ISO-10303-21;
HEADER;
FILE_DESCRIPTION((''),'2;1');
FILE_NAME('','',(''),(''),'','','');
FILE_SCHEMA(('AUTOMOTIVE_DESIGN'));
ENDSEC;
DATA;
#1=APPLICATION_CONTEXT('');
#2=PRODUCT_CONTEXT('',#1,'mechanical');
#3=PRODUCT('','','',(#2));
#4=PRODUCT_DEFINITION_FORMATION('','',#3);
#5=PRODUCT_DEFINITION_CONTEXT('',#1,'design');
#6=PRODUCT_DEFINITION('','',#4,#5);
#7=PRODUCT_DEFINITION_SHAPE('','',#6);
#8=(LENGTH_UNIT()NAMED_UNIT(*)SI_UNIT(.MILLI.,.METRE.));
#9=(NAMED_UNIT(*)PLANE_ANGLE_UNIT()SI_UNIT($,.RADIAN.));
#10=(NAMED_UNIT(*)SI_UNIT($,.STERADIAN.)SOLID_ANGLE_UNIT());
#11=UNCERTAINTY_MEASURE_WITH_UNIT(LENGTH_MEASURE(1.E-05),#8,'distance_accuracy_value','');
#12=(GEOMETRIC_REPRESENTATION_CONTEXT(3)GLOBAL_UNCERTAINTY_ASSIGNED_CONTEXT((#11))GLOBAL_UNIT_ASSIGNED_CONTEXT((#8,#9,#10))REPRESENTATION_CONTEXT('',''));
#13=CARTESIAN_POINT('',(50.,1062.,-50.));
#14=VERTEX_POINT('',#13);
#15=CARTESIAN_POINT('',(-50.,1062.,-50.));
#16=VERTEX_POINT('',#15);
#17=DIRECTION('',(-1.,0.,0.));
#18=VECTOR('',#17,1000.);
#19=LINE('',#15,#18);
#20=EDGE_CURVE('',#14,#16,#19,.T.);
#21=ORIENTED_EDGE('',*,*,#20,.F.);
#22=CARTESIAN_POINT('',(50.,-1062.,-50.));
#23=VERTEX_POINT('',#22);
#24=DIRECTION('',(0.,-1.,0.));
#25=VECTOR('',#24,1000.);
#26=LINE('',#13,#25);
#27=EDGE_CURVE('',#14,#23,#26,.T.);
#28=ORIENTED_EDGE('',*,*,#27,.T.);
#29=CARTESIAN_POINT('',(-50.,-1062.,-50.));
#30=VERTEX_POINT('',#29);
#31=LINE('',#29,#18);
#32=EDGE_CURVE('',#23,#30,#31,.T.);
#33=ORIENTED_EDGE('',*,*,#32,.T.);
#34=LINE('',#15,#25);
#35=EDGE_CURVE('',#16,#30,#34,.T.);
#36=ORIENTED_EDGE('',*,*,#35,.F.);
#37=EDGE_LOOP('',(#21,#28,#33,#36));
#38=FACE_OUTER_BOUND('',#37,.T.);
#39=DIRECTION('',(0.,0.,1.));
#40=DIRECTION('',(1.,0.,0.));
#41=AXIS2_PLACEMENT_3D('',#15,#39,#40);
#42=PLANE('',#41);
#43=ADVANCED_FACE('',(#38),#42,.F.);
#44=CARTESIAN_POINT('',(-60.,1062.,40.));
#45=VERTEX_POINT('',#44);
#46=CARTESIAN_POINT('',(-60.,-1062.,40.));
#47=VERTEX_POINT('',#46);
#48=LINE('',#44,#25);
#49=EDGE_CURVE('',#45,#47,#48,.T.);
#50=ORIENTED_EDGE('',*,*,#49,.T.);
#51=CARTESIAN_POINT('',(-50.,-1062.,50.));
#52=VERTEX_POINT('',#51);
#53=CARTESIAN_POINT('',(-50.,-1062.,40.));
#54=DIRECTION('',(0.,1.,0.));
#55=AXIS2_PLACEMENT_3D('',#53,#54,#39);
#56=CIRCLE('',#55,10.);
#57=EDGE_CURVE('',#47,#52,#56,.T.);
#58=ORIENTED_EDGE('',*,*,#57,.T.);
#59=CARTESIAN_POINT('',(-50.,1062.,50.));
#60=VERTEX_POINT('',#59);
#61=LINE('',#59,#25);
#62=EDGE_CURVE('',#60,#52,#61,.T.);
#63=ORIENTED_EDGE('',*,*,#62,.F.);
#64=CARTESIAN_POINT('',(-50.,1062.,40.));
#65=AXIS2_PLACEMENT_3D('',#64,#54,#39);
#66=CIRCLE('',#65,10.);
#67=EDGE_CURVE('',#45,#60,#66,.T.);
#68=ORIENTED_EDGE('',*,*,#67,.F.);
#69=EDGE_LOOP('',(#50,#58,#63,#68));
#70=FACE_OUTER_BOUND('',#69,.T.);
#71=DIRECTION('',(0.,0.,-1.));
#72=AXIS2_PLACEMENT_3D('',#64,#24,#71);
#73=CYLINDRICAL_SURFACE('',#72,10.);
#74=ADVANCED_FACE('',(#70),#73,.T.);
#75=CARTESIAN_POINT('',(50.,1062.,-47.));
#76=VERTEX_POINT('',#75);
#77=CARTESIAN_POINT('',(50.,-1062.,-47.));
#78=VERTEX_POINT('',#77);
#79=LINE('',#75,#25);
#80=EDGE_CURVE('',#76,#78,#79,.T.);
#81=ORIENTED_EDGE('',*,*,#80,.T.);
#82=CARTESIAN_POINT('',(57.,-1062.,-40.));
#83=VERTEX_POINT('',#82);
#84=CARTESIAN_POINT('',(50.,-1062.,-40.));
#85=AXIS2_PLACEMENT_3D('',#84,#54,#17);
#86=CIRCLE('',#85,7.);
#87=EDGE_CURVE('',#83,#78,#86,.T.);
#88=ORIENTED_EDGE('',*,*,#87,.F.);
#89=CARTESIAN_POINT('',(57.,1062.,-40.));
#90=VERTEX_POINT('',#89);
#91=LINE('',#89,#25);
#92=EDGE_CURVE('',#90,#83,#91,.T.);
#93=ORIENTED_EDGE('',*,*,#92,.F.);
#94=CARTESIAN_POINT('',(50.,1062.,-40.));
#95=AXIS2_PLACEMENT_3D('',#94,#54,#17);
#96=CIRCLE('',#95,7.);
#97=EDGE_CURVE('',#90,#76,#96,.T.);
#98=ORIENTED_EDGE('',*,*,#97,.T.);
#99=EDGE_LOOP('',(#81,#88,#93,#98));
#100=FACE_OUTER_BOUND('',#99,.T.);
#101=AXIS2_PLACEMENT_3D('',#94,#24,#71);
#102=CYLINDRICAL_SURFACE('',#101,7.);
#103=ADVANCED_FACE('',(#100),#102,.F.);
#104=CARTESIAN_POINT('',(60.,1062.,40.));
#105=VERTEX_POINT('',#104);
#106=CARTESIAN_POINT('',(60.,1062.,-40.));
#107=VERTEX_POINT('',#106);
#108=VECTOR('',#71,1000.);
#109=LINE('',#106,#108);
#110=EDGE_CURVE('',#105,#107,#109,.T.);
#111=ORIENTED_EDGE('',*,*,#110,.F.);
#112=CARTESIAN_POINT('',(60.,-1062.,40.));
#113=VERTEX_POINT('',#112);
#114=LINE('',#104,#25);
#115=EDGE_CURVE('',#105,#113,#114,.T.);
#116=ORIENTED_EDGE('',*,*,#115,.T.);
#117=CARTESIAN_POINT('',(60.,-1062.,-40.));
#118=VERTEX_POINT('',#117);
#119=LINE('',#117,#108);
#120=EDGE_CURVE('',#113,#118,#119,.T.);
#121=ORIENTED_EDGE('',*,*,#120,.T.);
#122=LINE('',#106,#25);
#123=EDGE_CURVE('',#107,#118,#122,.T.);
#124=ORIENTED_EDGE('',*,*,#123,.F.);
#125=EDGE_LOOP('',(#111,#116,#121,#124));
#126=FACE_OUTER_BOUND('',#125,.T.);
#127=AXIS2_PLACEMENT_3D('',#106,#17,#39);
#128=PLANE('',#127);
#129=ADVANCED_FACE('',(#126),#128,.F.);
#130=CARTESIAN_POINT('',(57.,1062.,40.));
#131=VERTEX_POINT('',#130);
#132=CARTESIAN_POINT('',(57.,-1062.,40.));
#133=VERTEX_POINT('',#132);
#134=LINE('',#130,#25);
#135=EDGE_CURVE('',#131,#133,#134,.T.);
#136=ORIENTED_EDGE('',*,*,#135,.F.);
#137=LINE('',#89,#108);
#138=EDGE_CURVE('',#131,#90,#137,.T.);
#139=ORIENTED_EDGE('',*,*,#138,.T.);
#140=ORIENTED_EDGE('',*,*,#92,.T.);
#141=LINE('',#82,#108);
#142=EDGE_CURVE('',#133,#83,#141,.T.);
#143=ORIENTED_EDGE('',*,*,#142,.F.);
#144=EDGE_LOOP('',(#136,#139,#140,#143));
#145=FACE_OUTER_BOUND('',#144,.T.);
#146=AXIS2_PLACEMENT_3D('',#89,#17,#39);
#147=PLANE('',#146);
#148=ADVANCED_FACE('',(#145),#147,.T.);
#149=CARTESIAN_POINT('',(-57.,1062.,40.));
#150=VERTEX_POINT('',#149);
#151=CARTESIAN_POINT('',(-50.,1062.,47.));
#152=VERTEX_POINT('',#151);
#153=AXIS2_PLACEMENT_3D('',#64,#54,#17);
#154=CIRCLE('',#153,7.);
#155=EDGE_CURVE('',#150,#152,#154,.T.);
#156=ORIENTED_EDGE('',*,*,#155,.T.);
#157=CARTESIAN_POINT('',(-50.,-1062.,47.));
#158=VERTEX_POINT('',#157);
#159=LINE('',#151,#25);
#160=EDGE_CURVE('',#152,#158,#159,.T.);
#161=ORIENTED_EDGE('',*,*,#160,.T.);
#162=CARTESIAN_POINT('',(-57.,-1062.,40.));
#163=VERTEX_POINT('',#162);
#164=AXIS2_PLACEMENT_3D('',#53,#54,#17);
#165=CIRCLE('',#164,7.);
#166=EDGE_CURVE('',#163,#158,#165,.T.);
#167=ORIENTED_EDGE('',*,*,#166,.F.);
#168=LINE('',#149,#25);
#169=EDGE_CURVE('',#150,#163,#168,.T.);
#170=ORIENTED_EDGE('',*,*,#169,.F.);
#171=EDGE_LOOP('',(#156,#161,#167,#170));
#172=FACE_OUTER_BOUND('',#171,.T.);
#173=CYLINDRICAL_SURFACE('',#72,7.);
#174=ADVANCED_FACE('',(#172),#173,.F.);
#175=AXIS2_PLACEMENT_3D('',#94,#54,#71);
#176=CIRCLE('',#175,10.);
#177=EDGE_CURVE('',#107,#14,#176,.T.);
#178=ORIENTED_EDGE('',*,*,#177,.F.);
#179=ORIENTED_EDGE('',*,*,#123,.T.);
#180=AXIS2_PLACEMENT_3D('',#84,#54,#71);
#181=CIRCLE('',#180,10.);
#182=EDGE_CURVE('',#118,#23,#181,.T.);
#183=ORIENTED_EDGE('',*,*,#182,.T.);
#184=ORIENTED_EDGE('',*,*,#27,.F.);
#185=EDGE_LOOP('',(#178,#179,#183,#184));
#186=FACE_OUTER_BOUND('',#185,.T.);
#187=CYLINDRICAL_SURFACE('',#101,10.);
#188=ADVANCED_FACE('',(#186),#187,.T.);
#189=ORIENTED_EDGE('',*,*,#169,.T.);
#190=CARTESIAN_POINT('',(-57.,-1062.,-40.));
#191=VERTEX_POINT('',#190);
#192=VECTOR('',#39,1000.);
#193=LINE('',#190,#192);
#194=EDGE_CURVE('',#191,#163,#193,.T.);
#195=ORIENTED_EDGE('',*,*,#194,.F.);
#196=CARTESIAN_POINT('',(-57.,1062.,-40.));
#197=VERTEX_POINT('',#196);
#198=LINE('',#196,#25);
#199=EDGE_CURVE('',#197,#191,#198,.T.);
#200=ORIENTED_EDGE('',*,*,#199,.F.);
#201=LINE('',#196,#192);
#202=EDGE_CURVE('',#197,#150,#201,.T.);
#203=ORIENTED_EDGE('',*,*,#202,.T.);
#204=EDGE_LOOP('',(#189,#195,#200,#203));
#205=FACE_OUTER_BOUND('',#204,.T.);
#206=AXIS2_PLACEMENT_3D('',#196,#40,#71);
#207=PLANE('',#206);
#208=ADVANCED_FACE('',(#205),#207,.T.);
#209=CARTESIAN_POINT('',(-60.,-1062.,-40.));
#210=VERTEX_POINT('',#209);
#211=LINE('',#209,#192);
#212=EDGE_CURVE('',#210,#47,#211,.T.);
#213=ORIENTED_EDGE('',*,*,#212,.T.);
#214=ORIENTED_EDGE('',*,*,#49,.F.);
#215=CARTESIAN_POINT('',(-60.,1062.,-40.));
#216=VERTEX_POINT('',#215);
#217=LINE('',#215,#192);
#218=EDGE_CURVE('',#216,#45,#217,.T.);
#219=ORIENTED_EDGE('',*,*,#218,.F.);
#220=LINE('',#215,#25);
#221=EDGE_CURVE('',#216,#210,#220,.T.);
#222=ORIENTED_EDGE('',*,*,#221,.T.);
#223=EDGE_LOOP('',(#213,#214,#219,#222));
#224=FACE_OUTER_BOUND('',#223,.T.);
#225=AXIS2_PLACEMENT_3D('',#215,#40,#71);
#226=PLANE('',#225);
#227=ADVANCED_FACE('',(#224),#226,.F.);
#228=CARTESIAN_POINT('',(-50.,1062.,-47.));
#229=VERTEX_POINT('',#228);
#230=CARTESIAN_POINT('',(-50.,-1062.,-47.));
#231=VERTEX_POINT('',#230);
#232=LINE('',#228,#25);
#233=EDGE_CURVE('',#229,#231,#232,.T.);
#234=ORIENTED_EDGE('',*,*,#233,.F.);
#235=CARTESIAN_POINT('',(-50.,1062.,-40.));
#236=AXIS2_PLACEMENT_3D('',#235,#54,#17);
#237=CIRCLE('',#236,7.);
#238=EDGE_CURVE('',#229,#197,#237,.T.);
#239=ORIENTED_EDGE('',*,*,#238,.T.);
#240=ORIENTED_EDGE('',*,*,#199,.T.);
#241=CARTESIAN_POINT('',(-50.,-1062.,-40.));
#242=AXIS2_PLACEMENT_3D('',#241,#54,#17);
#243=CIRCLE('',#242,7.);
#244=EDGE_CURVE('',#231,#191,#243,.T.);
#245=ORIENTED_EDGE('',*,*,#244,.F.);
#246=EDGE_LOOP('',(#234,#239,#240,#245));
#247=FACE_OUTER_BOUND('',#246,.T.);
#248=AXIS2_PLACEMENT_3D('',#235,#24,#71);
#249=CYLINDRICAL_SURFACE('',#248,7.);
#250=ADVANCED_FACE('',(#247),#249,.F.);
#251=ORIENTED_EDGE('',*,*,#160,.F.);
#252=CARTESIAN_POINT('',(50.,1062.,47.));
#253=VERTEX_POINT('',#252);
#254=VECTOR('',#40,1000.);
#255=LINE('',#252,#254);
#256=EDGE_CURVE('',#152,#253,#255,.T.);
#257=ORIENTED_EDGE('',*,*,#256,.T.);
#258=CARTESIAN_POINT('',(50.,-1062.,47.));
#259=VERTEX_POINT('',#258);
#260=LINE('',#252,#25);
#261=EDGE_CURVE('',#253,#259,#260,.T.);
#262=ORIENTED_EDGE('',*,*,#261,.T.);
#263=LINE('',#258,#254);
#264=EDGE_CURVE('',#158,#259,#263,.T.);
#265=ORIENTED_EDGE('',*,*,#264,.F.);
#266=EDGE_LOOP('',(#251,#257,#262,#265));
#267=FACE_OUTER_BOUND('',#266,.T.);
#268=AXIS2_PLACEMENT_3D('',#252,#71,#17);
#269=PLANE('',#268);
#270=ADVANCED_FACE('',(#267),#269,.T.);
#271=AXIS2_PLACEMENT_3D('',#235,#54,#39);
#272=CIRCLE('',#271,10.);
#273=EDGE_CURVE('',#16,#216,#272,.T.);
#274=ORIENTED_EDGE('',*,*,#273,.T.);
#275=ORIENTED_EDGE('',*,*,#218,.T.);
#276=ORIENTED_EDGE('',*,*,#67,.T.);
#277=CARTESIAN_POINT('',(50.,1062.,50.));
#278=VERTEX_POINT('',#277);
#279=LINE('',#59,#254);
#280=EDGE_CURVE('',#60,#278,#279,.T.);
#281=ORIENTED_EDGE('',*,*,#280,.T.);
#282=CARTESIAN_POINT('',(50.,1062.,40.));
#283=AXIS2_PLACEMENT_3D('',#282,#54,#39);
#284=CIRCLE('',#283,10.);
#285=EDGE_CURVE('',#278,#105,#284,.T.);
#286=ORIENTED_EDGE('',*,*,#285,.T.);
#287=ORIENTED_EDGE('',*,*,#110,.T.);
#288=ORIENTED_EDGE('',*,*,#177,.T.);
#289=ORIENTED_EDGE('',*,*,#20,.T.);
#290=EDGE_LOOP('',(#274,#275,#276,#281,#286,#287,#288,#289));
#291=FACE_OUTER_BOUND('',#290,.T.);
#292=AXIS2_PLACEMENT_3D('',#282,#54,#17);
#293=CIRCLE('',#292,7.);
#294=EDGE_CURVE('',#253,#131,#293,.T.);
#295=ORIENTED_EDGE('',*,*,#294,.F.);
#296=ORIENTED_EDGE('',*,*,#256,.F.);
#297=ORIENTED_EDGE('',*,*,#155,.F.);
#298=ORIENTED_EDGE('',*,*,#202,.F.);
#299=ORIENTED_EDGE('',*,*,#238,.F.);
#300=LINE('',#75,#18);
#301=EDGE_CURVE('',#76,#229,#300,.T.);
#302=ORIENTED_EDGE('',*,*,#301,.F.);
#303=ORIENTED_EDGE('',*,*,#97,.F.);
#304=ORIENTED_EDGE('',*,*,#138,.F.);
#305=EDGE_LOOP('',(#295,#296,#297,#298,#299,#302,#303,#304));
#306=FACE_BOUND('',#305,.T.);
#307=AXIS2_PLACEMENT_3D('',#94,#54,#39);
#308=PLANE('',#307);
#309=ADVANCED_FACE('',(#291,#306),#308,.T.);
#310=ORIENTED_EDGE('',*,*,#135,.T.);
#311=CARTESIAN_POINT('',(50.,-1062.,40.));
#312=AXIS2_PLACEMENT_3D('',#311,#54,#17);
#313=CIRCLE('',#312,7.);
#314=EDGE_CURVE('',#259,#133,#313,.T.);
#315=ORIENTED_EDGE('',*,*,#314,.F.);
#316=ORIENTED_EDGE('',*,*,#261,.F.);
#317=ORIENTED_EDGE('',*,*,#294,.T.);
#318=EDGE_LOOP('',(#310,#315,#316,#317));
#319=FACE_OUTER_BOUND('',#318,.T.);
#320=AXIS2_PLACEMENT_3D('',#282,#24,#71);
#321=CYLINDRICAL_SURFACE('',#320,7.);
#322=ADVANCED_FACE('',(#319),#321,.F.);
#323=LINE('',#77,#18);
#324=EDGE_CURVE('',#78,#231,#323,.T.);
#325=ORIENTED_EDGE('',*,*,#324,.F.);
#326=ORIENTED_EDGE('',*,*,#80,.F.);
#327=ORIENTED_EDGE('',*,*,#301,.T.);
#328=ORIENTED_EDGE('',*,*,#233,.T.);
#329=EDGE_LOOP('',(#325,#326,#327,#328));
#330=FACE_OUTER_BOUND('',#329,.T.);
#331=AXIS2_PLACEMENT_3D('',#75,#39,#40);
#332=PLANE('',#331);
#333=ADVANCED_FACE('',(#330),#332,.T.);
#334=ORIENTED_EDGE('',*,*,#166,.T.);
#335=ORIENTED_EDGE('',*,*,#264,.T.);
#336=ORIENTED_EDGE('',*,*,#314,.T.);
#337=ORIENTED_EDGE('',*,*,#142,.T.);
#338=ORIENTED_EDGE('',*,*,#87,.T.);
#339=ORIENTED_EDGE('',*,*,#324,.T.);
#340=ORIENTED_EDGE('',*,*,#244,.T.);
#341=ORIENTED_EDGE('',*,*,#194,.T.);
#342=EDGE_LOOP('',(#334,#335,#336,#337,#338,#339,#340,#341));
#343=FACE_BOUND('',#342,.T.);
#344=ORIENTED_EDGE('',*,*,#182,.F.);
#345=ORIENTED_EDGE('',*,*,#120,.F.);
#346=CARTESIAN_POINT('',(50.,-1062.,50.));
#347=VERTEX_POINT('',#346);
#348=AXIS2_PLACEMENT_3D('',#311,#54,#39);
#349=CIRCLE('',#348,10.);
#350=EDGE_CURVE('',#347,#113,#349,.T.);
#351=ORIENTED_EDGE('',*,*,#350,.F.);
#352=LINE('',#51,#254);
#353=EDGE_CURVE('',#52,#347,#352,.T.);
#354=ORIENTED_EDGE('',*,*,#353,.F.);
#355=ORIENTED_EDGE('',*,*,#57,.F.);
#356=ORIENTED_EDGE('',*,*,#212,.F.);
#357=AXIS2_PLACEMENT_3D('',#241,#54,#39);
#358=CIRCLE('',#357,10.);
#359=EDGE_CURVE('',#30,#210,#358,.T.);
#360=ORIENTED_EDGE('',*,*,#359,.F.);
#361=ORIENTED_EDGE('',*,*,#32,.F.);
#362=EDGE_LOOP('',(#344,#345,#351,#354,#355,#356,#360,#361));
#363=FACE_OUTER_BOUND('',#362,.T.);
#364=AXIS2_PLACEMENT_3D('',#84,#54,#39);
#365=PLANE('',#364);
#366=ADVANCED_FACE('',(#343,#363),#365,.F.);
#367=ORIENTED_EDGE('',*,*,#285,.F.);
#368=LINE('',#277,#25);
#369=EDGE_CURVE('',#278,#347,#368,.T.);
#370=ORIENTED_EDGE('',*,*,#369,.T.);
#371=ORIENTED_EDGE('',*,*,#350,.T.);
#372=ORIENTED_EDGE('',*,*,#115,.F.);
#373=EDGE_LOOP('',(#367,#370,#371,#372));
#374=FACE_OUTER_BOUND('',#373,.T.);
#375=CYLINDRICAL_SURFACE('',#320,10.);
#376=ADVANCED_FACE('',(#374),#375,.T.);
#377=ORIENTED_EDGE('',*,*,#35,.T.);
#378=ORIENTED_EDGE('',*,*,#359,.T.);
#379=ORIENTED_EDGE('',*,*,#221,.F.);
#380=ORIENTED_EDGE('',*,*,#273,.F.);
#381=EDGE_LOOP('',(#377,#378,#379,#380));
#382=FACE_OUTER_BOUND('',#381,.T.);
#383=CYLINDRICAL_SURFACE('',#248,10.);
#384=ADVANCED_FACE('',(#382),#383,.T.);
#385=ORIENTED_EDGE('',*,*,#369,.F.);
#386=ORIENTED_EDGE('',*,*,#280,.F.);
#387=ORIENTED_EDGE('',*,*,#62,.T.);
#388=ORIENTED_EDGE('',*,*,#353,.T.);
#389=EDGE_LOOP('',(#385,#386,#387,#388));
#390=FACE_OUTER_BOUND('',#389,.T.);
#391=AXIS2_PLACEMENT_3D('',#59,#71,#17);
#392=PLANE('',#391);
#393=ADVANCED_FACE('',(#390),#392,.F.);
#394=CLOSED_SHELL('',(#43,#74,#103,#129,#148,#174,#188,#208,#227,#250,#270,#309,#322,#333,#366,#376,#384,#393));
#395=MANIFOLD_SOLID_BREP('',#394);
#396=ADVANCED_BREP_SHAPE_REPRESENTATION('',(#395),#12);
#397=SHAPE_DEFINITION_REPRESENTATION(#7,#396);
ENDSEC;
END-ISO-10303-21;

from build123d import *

# Parameters (mm, degrees)
EXTRUDE_THIN1_DEPTH = 1062


with BuildPart() as part:
    # Sketch1 → Extrude-Thin1 (new, symmetric)
    with BuildSketch(Plane(origin=(0, 0, 0), x_dir=(1, 0, 0), z_dir=(0, 1, 0))):
        with BuildLine():
            Line((-50, 50), (50, 50))
            ThreePointArc((50, 50), (57.071067812, 47.071067812), (60, 40))
            Line((60, 40), (60, -40))
            ThreePointArc((60, -40), (57.071067812, -47.071067812), (50, -50))
            Line((50, -50), (-50, -50))
            ThreePointArc((-50, -50), (-57.071067812, -47.071067812), (-60, -40))
            Line((-60, -40), (-60, 40))
            ThreePointArc((-60, 40), (-57.071067812, 47.071067812), (-50, 50))
        make_face()
        with BuildLine():
            Line((-50, 47), (50, 47))
            ThreePointArc((50, 47), (54.949747468, 44.949747468), (57, 40))
            Line((57, 40), (57, -40))
            ThreePointArc((57, -40), (54.949747468, -44.949747468), (50, -47))
            Line((50, -47), (-50, -47))
            ThreePointArc((-50, -47), (-54.949747468, -44.949747468), (-57, -40))
            Line((-57, -40), (-57, 40))
            ThreePointArc((-57, 40), (-54.949747468, 44.949747468), (-50, 47))
        make_face(mode=Mode.SUBTRACT)
    extrude(amount=EXTRUDE_THIN1_DEPTH, both=True)


solid = part.part
